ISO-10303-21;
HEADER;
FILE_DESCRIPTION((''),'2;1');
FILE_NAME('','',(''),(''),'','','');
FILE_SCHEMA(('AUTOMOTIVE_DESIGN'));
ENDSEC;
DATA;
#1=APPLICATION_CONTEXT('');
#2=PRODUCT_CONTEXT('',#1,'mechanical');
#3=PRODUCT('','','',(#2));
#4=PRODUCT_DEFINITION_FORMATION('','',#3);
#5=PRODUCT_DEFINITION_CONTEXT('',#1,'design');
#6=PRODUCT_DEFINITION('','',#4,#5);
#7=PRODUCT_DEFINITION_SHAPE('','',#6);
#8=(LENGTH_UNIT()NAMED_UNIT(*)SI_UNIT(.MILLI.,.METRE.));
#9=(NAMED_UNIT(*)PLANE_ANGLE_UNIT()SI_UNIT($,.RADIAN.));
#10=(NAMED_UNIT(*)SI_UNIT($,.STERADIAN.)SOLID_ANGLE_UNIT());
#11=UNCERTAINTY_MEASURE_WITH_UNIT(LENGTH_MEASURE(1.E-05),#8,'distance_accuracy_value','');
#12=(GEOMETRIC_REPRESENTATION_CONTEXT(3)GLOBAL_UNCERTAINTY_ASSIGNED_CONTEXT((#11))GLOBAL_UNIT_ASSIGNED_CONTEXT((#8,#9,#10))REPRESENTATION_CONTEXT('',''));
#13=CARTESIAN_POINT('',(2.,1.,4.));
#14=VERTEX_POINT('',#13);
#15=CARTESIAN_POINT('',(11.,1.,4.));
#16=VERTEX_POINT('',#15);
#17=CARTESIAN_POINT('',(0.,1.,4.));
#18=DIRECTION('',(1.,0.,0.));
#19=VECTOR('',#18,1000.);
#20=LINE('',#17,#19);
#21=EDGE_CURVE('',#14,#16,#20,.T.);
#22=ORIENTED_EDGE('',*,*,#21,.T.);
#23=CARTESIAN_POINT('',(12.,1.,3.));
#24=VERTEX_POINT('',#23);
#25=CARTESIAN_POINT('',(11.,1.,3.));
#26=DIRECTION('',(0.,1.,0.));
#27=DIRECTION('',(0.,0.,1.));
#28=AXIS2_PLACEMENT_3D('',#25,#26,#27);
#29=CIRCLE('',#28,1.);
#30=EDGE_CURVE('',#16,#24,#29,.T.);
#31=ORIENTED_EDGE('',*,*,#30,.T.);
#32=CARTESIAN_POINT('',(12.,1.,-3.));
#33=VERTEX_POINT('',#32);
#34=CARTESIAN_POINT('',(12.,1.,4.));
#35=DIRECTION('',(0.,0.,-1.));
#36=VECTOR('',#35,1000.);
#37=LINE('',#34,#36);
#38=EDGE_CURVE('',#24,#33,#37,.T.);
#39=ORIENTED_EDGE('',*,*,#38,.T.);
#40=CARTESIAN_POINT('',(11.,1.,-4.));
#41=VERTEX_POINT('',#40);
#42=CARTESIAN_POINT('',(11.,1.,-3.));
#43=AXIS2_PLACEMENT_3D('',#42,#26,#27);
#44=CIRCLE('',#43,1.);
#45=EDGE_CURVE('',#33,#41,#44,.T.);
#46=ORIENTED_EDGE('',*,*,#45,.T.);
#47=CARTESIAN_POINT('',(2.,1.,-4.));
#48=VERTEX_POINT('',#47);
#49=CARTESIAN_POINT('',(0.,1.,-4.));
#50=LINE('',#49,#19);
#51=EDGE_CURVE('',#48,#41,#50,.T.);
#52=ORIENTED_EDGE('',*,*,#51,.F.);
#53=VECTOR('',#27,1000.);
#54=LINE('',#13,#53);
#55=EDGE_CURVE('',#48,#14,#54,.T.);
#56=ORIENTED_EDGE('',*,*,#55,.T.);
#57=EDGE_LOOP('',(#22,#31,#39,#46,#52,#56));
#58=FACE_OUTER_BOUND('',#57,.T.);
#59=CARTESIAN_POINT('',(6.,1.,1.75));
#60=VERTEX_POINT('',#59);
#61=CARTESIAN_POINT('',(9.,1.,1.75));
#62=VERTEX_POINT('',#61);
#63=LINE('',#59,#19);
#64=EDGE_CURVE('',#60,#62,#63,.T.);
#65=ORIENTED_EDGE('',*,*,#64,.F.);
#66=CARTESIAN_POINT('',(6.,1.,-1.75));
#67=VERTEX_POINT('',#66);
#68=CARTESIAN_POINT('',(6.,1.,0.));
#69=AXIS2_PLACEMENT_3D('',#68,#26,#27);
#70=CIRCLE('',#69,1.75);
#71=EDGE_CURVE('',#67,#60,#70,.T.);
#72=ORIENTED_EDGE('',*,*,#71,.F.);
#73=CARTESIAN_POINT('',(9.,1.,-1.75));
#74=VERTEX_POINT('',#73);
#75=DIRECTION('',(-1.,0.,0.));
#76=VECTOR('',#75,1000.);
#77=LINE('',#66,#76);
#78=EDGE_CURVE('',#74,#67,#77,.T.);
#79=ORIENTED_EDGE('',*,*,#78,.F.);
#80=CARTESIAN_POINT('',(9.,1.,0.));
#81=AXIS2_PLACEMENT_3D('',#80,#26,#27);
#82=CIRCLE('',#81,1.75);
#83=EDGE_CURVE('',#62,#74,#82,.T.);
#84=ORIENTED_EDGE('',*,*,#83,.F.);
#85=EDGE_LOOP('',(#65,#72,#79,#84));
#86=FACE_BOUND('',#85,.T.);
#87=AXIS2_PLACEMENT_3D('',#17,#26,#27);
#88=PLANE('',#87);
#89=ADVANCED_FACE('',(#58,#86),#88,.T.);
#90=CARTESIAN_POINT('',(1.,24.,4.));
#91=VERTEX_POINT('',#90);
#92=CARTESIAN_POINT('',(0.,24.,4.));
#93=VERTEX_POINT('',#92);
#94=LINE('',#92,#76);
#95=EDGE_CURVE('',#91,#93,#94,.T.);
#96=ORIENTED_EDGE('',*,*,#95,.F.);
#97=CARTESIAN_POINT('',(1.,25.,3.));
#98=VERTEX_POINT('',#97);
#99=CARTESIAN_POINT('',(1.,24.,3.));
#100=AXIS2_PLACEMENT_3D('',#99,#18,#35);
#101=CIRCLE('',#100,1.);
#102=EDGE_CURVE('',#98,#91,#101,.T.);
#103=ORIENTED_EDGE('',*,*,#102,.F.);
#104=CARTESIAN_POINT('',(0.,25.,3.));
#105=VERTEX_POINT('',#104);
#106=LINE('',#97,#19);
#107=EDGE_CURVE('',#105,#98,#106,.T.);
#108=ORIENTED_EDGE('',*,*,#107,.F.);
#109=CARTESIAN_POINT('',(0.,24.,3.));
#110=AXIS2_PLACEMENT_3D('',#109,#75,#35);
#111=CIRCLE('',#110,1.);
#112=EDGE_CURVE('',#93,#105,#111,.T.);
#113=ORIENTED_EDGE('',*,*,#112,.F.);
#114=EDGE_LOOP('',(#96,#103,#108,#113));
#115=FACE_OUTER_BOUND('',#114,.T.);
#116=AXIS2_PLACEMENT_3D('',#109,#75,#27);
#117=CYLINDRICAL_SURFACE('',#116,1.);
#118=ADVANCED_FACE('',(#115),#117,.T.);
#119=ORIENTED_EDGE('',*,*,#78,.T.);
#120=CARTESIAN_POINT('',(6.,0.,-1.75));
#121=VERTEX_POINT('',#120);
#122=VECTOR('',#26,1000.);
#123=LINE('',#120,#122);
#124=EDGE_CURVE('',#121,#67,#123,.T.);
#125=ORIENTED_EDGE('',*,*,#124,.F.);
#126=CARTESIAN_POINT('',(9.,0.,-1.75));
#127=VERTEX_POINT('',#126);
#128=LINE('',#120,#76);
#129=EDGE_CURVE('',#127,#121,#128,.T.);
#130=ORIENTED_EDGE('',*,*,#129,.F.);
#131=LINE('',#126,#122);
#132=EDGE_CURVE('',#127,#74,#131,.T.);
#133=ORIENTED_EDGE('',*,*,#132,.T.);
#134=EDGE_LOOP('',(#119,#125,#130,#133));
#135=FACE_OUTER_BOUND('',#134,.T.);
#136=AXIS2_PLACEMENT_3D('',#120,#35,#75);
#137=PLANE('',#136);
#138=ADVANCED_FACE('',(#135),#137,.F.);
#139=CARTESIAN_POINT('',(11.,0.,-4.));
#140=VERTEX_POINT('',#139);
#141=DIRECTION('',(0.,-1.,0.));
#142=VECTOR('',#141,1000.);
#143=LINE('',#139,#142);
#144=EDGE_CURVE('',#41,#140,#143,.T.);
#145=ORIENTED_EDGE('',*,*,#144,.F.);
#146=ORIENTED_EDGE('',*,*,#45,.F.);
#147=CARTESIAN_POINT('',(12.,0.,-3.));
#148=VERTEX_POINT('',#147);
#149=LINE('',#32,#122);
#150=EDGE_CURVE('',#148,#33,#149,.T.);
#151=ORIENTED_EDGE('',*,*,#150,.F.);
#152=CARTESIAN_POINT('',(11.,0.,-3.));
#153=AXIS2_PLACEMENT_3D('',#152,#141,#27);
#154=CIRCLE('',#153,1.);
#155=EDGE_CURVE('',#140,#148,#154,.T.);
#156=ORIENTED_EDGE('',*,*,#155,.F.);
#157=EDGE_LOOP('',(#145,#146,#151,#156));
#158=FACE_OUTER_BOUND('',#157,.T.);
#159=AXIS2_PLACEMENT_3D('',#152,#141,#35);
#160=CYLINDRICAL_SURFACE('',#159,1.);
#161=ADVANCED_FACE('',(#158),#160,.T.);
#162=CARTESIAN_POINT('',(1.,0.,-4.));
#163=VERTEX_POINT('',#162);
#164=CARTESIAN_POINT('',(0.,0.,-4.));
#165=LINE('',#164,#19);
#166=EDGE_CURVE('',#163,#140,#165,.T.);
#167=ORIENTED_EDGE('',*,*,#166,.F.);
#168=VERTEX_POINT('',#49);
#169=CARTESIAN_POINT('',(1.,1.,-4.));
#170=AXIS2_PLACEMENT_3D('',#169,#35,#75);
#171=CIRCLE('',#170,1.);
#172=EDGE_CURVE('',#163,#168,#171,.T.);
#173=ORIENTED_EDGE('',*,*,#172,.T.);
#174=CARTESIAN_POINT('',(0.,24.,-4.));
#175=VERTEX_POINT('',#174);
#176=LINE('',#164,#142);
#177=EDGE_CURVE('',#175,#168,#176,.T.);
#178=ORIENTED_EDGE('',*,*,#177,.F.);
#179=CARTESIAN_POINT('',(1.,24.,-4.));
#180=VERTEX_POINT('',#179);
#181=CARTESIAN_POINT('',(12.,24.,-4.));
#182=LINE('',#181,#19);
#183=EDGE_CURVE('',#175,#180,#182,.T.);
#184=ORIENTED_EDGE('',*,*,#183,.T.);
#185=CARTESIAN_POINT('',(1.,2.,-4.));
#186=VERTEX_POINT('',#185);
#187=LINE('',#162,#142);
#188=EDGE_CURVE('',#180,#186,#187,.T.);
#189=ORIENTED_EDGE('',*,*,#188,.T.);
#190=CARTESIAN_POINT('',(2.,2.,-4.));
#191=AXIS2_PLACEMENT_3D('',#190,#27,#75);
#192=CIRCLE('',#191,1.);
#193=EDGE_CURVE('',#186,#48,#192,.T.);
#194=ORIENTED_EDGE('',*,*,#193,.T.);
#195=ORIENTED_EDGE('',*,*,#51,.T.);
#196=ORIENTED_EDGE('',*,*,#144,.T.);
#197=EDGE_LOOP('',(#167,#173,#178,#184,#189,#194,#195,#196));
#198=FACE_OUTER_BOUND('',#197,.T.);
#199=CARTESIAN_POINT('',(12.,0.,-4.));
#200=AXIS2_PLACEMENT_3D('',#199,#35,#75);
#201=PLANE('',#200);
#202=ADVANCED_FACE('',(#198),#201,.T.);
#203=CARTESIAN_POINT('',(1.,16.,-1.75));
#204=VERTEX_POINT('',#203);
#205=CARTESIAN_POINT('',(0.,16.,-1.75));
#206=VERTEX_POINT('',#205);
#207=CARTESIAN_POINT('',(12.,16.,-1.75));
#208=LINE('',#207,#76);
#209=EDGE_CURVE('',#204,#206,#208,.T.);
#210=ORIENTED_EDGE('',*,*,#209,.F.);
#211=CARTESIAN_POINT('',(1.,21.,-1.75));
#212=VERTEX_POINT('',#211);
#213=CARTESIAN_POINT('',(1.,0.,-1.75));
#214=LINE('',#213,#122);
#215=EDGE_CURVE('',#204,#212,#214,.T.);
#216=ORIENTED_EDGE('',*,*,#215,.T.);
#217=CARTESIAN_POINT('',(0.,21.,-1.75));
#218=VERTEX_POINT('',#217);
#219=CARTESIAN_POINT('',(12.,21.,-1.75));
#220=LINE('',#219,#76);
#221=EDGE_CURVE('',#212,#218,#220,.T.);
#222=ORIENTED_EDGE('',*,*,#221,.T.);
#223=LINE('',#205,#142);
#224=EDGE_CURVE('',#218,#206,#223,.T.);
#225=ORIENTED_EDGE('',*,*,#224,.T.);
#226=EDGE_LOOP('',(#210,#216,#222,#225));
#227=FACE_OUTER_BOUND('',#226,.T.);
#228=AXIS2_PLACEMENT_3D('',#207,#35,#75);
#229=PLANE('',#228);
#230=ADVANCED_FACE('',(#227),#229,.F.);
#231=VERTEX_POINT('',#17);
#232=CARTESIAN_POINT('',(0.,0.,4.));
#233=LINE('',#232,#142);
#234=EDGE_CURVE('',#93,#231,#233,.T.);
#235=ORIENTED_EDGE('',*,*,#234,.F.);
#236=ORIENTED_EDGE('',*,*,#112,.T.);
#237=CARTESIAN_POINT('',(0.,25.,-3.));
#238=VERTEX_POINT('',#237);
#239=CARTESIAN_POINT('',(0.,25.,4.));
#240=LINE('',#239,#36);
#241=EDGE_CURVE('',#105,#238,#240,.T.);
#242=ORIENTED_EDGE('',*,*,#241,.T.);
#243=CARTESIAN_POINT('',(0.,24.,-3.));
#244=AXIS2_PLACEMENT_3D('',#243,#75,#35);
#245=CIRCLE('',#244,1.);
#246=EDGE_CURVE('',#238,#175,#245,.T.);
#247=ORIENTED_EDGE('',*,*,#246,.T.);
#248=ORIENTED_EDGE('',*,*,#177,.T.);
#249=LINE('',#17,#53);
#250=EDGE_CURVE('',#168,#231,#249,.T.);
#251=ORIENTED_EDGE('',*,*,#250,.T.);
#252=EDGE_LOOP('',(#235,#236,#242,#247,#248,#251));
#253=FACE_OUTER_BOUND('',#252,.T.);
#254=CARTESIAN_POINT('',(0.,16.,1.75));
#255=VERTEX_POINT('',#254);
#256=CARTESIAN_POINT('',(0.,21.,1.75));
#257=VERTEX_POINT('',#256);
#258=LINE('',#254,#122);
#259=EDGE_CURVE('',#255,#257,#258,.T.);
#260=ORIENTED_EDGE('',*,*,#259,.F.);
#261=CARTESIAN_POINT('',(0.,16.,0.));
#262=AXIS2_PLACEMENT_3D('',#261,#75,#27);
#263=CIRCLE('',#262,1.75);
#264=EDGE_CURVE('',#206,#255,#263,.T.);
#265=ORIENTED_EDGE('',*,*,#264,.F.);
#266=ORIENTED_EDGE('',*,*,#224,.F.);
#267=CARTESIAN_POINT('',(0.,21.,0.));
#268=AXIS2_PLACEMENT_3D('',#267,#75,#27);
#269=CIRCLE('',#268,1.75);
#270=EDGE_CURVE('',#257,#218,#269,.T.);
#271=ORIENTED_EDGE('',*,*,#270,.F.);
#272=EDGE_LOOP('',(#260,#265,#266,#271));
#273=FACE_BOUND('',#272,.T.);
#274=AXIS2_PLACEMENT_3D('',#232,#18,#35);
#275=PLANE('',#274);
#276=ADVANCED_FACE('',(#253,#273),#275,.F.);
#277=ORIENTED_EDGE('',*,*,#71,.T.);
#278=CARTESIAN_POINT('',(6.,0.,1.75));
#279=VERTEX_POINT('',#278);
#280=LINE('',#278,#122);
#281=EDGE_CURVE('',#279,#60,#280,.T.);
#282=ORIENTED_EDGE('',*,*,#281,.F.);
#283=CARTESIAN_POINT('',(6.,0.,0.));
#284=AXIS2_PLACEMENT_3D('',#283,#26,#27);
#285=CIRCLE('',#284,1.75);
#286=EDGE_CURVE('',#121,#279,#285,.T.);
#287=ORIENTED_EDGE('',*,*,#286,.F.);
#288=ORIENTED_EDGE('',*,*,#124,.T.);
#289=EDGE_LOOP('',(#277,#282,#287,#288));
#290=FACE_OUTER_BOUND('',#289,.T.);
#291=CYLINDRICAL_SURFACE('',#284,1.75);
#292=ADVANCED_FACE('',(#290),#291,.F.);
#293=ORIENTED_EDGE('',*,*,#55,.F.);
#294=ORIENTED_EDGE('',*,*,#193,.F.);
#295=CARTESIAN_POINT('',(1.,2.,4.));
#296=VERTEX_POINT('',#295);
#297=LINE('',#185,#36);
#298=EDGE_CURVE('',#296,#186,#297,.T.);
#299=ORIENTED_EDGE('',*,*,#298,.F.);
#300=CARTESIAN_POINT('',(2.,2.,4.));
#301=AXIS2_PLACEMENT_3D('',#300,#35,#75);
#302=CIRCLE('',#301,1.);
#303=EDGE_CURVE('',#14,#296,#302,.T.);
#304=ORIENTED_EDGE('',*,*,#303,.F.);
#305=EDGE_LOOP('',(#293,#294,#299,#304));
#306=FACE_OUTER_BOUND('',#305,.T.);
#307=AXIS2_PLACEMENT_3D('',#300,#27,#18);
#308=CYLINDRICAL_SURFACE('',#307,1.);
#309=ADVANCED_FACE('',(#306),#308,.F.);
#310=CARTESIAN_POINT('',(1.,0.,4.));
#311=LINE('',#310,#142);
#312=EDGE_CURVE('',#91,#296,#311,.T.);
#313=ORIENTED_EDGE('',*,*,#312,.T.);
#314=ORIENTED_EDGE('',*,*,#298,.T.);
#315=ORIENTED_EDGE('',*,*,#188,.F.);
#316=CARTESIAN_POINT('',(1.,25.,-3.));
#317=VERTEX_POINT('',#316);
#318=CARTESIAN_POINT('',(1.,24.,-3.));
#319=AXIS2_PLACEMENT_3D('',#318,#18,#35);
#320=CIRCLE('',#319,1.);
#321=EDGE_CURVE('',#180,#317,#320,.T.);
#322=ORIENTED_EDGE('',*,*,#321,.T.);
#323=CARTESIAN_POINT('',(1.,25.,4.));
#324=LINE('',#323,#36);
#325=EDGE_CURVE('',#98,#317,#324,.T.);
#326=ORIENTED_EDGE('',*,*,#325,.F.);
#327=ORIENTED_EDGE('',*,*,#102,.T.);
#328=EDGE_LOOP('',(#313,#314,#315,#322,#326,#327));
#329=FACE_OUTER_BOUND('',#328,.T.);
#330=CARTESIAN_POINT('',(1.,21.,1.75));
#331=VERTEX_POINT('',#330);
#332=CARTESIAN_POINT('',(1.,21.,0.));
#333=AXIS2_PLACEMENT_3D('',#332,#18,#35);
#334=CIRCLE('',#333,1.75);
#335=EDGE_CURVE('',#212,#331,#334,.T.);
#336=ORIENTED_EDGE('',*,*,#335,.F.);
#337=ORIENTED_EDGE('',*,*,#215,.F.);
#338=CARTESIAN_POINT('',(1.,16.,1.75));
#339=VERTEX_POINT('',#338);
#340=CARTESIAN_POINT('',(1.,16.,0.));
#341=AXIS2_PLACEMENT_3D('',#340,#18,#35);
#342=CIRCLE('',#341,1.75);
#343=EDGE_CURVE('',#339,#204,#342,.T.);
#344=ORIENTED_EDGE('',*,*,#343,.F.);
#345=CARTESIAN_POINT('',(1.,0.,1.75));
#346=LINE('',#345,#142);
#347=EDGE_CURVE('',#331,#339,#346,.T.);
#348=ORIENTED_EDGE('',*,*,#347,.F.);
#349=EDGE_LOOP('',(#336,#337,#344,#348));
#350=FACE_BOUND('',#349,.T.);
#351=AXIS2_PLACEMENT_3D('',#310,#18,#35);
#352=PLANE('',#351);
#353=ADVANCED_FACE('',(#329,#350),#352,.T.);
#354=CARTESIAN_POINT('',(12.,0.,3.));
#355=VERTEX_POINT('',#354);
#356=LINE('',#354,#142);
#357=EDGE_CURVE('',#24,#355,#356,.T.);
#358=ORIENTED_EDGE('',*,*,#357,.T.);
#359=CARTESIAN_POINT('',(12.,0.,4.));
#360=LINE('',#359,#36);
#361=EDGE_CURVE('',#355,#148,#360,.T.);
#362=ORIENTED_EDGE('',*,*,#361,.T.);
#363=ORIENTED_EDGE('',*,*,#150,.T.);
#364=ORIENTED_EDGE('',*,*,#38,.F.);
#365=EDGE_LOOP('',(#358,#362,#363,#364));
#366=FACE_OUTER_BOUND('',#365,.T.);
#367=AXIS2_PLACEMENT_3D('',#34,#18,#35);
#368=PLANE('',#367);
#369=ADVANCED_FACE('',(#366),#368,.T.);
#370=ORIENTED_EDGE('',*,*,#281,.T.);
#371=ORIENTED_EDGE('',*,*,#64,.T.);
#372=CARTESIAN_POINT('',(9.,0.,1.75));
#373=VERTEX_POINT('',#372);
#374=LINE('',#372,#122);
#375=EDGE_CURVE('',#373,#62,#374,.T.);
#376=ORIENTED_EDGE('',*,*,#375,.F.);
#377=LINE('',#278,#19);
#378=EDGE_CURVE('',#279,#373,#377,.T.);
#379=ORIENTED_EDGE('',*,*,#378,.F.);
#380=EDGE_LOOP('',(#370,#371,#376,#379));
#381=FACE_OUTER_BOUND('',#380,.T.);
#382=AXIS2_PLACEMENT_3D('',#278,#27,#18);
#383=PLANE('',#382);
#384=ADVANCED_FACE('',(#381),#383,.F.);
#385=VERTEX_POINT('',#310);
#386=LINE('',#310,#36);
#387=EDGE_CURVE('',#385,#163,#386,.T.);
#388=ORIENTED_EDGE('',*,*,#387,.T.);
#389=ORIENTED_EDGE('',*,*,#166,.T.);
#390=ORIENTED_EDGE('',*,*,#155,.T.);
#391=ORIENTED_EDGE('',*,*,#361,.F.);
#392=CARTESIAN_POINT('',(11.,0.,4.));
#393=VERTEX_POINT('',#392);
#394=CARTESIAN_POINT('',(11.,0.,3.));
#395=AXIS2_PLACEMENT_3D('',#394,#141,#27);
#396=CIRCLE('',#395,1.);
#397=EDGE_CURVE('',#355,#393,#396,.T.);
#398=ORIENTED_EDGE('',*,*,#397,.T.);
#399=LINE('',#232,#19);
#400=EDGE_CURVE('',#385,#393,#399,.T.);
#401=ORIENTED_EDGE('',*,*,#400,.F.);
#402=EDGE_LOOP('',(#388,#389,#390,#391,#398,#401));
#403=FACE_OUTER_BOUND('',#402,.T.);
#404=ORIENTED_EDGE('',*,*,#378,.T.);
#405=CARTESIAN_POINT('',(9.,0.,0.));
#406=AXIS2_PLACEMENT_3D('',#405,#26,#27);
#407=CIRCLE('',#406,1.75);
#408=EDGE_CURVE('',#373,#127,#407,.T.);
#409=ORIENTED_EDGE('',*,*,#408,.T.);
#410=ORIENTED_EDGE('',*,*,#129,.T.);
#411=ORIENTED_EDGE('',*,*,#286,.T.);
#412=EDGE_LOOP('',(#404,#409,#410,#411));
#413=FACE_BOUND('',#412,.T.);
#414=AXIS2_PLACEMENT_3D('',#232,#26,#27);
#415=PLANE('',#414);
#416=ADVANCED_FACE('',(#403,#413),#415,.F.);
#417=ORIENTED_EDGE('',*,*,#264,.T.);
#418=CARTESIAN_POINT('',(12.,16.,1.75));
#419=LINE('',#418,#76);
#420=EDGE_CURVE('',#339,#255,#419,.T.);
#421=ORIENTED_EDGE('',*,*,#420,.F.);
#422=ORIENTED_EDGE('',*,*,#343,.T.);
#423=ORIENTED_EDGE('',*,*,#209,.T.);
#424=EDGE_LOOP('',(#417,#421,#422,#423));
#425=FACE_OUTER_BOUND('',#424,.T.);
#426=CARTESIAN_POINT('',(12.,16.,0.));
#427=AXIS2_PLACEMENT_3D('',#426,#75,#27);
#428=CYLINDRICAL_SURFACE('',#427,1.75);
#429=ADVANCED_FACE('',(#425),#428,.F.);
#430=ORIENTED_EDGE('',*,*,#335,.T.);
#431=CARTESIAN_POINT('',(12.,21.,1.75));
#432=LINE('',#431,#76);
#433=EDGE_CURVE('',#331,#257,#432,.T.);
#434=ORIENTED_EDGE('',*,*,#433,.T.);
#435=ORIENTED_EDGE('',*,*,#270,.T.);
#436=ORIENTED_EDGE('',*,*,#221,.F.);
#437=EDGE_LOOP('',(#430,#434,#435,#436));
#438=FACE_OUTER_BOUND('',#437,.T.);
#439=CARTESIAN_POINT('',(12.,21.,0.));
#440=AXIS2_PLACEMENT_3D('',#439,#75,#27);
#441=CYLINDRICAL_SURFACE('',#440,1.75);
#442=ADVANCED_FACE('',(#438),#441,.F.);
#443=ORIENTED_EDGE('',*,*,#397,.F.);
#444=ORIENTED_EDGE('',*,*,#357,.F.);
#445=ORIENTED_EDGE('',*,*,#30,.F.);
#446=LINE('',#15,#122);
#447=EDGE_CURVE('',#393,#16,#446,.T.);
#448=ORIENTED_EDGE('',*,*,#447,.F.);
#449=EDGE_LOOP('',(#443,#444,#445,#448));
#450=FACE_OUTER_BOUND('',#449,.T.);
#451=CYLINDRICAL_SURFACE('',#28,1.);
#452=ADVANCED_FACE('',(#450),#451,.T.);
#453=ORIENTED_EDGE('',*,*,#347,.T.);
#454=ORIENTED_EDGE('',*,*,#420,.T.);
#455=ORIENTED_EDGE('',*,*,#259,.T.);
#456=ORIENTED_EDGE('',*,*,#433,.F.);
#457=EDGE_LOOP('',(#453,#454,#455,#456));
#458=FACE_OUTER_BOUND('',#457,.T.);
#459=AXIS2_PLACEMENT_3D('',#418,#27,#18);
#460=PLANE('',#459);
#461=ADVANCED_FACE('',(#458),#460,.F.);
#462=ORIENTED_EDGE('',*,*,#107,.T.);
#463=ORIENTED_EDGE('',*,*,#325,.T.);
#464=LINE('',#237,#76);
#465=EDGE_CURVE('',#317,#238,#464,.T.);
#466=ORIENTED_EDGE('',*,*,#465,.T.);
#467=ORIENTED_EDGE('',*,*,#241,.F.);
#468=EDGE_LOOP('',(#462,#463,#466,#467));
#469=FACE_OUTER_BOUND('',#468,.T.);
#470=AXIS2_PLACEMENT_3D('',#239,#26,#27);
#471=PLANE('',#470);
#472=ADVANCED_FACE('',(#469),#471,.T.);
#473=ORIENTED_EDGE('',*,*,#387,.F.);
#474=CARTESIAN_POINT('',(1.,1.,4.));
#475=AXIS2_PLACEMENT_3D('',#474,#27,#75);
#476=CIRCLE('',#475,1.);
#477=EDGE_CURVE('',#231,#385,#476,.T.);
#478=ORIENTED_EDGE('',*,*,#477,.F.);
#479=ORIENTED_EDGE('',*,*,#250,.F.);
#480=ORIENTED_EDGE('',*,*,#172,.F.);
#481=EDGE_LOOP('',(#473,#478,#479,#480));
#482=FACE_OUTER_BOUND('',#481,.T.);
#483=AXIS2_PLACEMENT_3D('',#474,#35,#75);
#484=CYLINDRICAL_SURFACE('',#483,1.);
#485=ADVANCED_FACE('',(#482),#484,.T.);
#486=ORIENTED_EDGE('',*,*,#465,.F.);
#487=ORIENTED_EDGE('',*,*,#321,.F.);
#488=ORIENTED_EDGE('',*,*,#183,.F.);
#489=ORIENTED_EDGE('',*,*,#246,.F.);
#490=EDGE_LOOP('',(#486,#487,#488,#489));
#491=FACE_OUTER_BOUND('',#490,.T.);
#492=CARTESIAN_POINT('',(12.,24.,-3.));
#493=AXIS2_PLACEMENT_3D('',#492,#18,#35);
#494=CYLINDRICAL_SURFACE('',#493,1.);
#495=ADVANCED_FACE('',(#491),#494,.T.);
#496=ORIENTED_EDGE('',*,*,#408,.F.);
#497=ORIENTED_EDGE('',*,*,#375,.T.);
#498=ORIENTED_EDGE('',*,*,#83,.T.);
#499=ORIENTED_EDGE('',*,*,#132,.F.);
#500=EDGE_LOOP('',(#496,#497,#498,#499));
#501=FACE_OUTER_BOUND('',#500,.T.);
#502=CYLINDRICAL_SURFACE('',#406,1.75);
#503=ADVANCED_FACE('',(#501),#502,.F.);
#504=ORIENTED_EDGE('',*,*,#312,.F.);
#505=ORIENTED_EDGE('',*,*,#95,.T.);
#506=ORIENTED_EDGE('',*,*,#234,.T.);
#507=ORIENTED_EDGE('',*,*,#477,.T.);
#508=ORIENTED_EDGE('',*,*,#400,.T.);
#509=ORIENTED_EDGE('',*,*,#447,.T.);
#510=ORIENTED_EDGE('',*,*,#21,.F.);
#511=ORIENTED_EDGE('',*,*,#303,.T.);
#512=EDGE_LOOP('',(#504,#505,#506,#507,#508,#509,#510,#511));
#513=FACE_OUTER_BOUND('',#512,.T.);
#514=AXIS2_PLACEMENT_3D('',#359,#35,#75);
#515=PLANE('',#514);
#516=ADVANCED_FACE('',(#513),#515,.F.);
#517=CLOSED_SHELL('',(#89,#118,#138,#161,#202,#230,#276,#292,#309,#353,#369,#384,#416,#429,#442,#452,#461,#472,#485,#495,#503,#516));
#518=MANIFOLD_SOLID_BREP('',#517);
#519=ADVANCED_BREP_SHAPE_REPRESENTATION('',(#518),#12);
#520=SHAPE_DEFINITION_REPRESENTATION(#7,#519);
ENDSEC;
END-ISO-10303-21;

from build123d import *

# Parameters (mm, degrees)
EXTRUDE_THIN1_DEPTH = 4
CUT_EXTRUDE1_DEPTH  = 28.129319933
CUT_EXTRUDE2_DEPTH  = 29.017851452
FILLET1_R           = 1


with BuildPart() as part:
    # Sketch1 → Extrude-Thin1 (new, symmetric)
    with BuildSketch(Plane.XY):
        Polygon((12, 0), (0, 0), (0, 25), (1, 25), (1, 1), (12, 1), align=None)
    extrude(amount=EXTRUDE_THIN1_DEPTH, both=True)

    # Sketch2 → Cut-Extrude1 (cut, through all)
    with BuildSketch(Plane(origin=(0, 1, 0), x_dir=(1, 0, 0), z_dir=(0, 1, 0))):
        with BuildLine():
            Line((6, 1.75), (9, 1.75))
            ThreePointArc((9, 1.75), (10.75, 0), (9, -1.75))
            Line((9, -1.75), (6, -1.75))
            ThreePointArc((6, -1.75), (4.25, 0), (6, 1.75))
        make_face()
    extrude(amount=-CUT_EXTRUDE1_DEPTH, mode=Mode.SUBTRACT)

    # Sketch3 → Cut-Extrude2 (cut, through all)
    with BuildSketch(Plane.ZY):
        with BuildLine():
            Line((-1.75, 16), (-1.75, 21))
            ThreePointArc((-1.75, 21), (0, 22.75), (1.75, 21))
            Line((1.75, 21), (1.75, 16))
            ThreePointArc((1.75, 16), (0, 14.25), (-1.75, 16))
        make_face()
    extrude(amount=-CUT_EXTRUDE2_DEPTH, mode=Mode.SUBTRACT)

    # Fillet1
    fillet1_edges = [part.edges().sort_by_distance(p)[0] for p in [
        (0.5, 25, 4),
        (0.5, 25, -4),
        (12, 0.5, -4),
        (12, 0.5, 4),
        (0, 0, 0),
        (1, 1, 0),
    ]]
    fillet(fillet1_edges, radius=FILLET1_R)


solid = part.part
